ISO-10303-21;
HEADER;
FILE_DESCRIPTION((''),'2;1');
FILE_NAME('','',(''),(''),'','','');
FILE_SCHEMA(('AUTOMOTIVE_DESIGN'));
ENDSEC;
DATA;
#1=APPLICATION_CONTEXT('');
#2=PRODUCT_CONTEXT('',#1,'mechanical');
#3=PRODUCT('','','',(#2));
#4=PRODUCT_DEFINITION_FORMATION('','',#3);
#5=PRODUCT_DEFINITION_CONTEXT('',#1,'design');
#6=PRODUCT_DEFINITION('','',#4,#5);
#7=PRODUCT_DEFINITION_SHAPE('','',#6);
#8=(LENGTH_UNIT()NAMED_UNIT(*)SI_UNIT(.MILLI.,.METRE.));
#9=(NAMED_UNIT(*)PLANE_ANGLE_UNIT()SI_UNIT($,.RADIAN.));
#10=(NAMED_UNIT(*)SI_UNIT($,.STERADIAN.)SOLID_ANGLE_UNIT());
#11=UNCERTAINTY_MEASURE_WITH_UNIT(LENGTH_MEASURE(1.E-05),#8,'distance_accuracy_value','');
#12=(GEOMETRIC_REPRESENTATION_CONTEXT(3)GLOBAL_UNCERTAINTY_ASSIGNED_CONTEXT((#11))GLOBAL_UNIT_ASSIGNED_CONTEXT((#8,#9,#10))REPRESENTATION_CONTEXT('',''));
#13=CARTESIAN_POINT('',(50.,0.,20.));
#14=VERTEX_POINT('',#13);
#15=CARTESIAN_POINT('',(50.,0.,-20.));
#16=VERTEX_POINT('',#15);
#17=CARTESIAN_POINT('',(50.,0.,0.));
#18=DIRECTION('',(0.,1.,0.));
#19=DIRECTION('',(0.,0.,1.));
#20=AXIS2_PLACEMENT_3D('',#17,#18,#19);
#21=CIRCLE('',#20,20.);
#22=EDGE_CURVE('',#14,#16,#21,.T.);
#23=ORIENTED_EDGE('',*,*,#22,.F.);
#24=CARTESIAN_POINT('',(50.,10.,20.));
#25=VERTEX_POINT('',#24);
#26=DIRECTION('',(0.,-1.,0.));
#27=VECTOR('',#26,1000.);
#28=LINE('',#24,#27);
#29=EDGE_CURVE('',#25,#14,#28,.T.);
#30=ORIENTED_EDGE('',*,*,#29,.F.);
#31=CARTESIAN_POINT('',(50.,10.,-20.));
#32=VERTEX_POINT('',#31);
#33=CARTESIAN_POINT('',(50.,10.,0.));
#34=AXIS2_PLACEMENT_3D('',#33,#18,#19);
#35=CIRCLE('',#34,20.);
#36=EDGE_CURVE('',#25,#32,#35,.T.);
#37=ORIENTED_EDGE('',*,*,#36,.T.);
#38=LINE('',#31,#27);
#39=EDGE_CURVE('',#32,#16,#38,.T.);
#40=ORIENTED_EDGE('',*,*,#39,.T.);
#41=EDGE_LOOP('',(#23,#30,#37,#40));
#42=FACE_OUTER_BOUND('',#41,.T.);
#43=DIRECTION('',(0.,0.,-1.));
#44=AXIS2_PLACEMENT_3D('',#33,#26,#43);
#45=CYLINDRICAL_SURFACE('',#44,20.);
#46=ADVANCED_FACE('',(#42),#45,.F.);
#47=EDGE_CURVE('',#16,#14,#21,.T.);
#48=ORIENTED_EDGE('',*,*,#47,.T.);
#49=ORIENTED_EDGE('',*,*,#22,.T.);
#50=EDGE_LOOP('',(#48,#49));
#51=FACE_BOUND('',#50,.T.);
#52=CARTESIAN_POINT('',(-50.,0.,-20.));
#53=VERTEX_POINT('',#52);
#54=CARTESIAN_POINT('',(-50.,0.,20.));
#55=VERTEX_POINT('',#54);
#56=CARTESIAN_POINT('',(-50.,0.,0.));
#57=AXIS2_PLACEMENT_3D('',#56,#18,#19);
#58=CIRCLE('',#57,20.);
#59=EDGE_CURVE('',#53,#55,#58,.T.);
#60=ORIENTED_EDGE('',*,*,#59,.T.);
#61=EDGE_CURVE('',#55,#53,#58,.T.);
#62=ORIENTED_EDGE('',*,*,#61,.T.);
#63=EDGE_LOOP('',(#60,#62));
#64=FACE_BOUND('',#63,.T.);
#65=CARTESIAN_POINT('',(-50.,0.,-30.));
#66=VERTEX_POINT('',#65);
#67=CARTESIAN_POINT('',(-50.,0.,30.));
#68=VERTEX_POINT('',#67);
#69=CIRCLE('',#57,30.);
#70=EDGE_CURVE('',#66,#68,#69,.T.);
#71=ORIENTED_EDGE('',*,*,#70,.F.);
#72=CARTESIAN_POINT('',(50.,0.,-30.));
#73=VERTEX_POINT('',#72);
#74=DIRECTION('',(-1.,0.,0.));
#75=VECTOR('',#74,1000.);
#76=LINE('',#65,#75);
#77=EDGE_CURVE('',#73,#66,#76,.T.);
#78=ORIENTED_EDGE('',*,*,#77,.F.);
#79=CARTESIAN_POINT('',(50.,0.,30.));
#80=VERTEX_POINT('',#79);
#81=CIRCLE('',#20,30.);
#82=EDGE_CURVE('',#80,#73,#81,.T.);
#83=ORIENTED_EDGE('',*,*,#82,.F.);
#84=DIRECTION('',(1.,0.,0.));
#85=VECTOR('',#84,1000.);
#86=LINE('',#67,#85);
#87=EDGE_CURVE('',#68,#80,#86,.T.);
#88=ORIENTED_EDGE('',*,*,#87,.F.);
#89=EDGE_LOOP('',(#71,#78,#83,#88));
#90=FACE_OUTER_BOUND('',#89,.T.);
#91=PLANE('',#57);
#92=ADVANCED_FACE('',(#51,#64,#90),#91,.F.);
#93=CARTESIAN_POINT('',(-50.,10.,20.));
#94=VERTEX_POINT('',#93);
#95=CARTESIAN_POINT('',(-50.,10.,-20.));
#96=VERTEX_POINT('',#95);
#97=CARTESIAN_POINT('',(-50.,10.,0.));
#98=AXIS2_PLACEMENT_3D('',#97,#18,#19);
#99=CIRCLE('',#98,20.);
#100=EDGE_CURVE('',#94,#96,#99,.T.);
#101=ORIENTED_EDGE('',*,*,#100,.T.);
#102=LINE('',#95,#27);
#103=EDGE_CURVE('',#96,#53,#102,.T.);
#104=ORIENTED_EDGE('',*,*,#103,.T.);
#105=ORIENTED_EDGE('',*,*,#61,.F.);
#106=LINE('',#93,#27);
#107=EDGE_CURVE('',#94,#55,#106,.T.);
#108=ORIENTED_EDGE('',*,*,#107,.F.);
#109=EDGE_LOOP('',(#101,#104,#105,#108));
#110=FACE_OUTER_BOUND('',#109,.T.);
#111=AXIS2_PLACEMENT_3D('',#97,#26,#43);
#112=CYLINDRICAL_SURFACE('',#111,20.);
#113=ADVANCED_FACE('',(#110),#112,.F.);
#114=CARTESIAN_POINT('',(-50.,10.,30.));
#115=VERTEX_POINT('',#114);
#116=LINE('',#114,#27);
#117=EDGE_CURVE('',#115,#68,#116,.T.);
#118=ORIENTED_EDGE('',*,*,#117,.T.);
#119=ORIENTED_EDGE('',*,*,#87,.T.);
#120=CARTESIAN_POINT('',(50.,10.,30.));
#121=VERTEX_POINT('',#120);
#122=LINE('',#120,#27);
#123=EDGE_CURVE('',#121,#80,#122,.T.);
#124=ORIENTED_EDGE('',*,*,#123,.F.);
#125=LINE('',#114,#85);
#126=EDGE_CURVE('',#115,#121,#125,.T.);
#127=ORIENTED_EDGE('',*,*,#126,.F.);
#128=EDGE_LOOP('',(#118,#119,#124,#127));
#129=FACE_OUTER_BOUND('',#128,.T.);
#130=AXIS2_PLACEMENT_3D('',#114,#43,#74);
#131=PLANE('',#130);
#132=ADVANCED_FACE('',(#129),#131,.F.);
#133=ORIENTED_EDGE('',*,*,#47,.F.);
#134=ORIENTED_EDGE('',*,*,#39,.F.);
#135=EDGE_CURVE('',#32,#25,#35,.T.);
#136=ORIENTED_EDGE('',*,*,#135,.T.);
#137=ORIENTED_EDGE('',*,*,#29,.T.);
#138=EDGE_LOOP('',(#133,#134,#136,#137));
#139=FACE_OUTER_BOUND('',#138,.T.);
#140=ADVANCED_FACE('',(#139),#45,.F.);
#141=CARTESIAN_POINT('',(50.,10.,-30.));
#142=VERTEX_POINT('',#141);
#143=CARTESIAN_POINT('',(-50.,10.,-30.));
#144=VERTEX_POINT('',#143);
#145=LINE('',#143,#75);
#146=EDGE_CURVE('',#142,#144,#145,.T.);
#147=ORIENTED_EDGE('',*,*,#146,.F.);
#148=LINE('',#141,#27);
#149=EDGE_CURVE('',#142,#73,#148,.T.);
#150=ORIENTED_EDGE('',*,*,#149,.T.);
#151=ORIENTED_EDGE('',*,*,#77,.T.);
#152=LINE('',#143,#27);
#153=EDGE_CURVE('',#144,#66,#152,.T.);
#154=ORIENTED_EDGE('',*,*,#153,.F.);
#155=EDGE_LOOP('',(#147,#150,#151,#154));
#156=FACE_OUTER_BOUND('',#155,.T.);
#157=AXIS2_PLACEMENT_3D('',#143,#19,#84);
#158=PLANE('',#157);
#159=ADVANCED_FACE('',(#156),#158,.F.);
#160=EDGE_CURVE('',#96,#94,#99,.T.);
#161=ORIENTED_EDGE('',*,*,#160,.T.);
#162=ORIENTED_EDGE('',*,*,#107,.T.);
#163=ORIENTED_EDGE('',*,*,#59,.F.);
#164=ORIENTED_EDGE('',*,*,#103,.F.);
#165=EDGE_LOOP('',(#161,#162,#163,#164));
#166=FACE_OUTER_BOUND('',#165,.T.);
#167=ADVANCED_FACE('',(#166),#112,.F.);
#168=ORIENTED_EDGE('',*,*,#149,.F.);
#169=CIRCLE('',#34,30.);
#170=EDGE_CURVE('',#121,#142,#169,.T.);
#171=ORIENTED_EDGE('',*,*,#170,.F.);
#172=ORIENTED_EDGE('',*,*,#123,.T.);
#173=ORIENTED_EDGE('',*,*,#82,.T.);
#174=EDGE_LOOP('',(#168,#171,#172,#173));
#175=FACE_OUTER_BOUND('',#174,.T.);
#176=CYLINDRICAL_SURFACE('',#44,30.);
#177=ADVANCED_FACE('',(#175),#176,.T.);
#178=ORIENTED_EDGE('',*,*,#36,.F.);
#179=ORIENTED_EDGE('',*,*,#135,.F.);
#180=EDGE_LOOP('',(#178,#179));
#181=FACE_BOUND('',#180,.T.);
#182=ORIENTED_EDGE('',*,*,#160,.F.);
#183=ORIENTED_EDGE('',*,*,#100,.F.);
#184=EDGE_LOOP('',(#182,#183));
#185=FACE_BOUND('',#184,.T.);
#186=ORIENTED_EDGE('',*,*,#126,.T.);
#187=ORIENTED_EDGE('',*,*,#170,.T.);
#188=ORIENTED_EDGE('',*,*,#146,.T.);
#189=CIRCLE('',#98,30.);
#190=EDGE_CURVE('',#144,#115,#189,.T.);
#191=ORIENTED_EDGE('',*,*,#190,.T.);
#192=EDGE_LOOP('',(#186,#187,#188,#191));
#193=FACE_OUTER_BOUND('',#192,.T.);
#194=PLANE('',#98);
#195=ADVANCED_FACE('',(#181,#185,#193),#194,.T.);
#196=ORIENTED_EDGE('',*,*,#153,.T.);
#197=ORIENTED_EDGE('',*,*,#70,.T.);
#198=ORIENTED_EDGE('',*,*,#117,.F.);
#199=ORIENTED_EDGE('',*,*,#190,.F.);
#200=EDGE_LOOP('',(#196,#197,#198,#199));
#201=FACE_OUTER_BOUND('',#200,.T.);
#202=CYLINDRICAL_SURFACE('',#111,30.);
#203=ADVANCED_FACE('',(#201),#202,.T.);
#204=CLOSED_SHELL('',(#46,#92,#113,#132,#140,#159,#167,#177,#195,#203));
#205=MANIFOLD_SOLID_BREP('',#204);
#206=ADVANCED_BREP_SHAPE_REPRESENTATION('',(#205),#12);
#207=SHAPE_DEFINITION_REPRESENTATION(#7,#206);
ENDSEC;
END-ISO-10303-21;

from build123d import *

# Parameters (mm, degrees)
SKETCH_1_R      = 20
EXTRUDE_1_DEPTH = 10


with BuildPart() as part:
    # 草图1 → 凸台-拉伸1 (new body)
    with BuildSketch(Plane(origin=(0, 0, 0), x_dir=(1, 0, 0), z_dir=(0, 1, 0))):
        with BuildLine():
            Line((-50, 30), (50, 30))
            ThreePointArc((50, 30), (80, 0), (50, -30))
            Line((50, -30), (-50, -30))
            ThreePointArc((-50, -30), (-80, 0), (-50, 30))
        make_face()
        with Locations(Location((50, 0, 0), (0, 0, 270))):
            Circle(SKETCH_1_R, mode=Mode.SUBTRACT)
        with Locations(Location((-50, 0, 0), (0, 0, 270))):
            Circle(SKETCH_1_R, mode=Mode.SUBTRACT)
    extrude(amount=EXTRUDE_1_DEPTH)


solid = part.part
